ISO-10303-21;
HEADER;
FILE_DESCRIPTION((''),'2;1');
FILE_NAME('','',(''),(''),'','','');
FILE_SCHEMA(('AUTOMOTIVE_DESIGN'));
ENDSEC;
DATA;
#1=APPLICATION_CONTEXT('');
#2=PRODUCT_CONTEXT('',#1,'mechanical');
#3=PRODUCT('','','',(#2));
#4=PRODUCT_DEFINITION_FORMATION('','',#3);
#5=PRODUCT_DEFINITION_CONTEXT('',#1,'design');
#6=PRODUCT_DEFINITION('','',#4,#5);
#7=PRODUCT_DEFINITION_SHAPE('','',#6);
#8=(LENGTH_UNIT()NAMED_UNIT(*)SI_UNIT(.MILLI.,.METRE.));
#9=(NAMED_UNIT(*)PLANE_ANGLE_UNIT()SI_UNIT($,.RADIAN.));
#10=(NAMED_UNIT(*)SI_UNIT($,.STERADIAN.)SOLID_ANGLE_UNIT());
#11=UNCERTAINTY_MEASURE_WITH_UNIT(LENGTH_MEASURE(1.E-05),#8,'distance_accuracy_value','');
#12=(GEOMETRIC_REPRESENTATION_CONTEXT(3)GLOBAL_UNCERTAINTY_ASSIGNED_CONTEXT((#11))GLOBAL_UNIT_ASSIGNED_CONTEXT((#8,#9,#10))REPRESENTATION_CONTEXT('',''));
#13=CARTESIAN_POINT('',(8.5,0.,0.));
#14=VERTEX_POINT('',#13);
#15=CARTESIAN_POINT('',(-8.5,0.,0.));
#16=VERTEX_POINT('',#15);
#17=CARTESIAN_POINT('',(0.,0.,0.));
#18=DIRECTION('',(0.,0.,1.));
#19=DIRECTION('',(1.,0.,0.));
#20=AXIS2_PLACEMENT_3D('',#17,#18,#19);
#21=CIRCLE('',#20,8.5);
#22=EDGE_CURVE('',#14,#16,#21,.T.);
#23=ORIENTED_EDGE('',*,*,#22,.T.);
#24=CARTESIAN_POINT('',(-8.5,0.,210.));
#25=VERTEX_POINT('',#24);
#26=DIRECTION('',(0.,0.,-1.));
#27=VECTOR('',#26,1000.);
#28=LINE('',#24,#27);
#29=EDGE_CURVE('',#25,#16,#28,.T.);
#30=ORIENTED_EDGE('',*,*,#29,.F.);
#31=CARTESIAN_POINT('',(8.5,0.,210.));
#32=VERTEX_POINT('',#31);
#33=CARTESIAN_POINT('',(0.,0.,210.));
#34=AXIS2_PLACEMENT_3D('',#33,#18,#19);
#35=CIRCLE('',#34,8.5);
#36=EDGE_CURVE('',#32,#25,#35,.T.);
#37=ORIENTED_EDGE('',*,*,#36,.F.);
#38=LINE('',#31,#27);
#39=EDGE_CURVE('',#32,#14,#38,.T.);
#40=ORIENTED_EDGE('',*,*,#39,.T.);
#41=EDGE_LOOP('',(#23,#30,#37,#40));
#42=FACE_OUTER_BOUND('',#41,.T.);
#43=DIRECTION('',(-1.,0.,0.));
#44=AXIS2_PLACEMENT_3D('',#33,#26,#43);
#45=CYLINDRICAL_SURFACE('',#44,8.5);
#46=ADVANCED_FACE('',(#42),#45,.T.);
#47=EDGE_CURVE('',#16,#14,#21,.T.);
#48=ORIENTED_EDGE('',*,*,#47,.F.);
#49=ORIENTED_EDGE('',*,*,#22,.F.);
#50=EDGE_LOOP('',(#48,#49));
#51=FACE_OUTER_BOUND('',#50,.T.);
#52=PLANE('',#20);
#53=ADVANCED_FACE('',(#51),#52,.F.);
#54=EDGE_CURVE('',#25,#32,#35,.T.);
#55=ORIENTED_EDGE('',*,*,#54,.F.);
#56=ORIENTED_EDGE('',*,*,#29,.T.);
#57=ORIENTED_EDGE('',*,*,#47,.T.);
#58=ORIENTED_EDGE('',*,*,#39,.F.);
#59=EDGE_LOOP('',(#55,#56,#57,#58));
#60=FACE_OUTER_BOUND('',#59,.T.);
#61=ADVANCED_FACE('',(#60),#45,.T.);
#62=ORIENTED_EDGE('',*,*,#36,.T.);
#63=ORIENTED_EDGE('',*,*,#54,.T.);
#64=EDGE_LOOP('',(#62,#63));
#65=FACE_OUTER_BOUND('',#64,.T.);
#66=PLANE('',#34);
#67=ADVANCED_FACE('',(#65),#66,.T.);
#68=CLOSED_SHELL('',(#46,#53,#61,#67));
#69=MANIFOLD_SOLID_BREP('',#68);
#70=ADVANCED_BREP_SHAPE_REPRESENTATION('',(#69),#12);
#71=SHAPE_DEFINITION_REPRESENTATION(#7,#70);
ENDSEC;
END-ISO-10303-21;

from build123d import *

# Parameters (mm, degrees)
SKETCH_1_R      = 8.5
EXTRUDE_1_DEPTH = 210


with BuildPart() as part:
    # 草图1 → 凸台-拉伸1 (new body)
    with BuildSketch(Plane.XY):
        Circle(SKETCH_1_R)
    extrude(amount=EXTRUDE_1_DEPTH)


solid = part.part
